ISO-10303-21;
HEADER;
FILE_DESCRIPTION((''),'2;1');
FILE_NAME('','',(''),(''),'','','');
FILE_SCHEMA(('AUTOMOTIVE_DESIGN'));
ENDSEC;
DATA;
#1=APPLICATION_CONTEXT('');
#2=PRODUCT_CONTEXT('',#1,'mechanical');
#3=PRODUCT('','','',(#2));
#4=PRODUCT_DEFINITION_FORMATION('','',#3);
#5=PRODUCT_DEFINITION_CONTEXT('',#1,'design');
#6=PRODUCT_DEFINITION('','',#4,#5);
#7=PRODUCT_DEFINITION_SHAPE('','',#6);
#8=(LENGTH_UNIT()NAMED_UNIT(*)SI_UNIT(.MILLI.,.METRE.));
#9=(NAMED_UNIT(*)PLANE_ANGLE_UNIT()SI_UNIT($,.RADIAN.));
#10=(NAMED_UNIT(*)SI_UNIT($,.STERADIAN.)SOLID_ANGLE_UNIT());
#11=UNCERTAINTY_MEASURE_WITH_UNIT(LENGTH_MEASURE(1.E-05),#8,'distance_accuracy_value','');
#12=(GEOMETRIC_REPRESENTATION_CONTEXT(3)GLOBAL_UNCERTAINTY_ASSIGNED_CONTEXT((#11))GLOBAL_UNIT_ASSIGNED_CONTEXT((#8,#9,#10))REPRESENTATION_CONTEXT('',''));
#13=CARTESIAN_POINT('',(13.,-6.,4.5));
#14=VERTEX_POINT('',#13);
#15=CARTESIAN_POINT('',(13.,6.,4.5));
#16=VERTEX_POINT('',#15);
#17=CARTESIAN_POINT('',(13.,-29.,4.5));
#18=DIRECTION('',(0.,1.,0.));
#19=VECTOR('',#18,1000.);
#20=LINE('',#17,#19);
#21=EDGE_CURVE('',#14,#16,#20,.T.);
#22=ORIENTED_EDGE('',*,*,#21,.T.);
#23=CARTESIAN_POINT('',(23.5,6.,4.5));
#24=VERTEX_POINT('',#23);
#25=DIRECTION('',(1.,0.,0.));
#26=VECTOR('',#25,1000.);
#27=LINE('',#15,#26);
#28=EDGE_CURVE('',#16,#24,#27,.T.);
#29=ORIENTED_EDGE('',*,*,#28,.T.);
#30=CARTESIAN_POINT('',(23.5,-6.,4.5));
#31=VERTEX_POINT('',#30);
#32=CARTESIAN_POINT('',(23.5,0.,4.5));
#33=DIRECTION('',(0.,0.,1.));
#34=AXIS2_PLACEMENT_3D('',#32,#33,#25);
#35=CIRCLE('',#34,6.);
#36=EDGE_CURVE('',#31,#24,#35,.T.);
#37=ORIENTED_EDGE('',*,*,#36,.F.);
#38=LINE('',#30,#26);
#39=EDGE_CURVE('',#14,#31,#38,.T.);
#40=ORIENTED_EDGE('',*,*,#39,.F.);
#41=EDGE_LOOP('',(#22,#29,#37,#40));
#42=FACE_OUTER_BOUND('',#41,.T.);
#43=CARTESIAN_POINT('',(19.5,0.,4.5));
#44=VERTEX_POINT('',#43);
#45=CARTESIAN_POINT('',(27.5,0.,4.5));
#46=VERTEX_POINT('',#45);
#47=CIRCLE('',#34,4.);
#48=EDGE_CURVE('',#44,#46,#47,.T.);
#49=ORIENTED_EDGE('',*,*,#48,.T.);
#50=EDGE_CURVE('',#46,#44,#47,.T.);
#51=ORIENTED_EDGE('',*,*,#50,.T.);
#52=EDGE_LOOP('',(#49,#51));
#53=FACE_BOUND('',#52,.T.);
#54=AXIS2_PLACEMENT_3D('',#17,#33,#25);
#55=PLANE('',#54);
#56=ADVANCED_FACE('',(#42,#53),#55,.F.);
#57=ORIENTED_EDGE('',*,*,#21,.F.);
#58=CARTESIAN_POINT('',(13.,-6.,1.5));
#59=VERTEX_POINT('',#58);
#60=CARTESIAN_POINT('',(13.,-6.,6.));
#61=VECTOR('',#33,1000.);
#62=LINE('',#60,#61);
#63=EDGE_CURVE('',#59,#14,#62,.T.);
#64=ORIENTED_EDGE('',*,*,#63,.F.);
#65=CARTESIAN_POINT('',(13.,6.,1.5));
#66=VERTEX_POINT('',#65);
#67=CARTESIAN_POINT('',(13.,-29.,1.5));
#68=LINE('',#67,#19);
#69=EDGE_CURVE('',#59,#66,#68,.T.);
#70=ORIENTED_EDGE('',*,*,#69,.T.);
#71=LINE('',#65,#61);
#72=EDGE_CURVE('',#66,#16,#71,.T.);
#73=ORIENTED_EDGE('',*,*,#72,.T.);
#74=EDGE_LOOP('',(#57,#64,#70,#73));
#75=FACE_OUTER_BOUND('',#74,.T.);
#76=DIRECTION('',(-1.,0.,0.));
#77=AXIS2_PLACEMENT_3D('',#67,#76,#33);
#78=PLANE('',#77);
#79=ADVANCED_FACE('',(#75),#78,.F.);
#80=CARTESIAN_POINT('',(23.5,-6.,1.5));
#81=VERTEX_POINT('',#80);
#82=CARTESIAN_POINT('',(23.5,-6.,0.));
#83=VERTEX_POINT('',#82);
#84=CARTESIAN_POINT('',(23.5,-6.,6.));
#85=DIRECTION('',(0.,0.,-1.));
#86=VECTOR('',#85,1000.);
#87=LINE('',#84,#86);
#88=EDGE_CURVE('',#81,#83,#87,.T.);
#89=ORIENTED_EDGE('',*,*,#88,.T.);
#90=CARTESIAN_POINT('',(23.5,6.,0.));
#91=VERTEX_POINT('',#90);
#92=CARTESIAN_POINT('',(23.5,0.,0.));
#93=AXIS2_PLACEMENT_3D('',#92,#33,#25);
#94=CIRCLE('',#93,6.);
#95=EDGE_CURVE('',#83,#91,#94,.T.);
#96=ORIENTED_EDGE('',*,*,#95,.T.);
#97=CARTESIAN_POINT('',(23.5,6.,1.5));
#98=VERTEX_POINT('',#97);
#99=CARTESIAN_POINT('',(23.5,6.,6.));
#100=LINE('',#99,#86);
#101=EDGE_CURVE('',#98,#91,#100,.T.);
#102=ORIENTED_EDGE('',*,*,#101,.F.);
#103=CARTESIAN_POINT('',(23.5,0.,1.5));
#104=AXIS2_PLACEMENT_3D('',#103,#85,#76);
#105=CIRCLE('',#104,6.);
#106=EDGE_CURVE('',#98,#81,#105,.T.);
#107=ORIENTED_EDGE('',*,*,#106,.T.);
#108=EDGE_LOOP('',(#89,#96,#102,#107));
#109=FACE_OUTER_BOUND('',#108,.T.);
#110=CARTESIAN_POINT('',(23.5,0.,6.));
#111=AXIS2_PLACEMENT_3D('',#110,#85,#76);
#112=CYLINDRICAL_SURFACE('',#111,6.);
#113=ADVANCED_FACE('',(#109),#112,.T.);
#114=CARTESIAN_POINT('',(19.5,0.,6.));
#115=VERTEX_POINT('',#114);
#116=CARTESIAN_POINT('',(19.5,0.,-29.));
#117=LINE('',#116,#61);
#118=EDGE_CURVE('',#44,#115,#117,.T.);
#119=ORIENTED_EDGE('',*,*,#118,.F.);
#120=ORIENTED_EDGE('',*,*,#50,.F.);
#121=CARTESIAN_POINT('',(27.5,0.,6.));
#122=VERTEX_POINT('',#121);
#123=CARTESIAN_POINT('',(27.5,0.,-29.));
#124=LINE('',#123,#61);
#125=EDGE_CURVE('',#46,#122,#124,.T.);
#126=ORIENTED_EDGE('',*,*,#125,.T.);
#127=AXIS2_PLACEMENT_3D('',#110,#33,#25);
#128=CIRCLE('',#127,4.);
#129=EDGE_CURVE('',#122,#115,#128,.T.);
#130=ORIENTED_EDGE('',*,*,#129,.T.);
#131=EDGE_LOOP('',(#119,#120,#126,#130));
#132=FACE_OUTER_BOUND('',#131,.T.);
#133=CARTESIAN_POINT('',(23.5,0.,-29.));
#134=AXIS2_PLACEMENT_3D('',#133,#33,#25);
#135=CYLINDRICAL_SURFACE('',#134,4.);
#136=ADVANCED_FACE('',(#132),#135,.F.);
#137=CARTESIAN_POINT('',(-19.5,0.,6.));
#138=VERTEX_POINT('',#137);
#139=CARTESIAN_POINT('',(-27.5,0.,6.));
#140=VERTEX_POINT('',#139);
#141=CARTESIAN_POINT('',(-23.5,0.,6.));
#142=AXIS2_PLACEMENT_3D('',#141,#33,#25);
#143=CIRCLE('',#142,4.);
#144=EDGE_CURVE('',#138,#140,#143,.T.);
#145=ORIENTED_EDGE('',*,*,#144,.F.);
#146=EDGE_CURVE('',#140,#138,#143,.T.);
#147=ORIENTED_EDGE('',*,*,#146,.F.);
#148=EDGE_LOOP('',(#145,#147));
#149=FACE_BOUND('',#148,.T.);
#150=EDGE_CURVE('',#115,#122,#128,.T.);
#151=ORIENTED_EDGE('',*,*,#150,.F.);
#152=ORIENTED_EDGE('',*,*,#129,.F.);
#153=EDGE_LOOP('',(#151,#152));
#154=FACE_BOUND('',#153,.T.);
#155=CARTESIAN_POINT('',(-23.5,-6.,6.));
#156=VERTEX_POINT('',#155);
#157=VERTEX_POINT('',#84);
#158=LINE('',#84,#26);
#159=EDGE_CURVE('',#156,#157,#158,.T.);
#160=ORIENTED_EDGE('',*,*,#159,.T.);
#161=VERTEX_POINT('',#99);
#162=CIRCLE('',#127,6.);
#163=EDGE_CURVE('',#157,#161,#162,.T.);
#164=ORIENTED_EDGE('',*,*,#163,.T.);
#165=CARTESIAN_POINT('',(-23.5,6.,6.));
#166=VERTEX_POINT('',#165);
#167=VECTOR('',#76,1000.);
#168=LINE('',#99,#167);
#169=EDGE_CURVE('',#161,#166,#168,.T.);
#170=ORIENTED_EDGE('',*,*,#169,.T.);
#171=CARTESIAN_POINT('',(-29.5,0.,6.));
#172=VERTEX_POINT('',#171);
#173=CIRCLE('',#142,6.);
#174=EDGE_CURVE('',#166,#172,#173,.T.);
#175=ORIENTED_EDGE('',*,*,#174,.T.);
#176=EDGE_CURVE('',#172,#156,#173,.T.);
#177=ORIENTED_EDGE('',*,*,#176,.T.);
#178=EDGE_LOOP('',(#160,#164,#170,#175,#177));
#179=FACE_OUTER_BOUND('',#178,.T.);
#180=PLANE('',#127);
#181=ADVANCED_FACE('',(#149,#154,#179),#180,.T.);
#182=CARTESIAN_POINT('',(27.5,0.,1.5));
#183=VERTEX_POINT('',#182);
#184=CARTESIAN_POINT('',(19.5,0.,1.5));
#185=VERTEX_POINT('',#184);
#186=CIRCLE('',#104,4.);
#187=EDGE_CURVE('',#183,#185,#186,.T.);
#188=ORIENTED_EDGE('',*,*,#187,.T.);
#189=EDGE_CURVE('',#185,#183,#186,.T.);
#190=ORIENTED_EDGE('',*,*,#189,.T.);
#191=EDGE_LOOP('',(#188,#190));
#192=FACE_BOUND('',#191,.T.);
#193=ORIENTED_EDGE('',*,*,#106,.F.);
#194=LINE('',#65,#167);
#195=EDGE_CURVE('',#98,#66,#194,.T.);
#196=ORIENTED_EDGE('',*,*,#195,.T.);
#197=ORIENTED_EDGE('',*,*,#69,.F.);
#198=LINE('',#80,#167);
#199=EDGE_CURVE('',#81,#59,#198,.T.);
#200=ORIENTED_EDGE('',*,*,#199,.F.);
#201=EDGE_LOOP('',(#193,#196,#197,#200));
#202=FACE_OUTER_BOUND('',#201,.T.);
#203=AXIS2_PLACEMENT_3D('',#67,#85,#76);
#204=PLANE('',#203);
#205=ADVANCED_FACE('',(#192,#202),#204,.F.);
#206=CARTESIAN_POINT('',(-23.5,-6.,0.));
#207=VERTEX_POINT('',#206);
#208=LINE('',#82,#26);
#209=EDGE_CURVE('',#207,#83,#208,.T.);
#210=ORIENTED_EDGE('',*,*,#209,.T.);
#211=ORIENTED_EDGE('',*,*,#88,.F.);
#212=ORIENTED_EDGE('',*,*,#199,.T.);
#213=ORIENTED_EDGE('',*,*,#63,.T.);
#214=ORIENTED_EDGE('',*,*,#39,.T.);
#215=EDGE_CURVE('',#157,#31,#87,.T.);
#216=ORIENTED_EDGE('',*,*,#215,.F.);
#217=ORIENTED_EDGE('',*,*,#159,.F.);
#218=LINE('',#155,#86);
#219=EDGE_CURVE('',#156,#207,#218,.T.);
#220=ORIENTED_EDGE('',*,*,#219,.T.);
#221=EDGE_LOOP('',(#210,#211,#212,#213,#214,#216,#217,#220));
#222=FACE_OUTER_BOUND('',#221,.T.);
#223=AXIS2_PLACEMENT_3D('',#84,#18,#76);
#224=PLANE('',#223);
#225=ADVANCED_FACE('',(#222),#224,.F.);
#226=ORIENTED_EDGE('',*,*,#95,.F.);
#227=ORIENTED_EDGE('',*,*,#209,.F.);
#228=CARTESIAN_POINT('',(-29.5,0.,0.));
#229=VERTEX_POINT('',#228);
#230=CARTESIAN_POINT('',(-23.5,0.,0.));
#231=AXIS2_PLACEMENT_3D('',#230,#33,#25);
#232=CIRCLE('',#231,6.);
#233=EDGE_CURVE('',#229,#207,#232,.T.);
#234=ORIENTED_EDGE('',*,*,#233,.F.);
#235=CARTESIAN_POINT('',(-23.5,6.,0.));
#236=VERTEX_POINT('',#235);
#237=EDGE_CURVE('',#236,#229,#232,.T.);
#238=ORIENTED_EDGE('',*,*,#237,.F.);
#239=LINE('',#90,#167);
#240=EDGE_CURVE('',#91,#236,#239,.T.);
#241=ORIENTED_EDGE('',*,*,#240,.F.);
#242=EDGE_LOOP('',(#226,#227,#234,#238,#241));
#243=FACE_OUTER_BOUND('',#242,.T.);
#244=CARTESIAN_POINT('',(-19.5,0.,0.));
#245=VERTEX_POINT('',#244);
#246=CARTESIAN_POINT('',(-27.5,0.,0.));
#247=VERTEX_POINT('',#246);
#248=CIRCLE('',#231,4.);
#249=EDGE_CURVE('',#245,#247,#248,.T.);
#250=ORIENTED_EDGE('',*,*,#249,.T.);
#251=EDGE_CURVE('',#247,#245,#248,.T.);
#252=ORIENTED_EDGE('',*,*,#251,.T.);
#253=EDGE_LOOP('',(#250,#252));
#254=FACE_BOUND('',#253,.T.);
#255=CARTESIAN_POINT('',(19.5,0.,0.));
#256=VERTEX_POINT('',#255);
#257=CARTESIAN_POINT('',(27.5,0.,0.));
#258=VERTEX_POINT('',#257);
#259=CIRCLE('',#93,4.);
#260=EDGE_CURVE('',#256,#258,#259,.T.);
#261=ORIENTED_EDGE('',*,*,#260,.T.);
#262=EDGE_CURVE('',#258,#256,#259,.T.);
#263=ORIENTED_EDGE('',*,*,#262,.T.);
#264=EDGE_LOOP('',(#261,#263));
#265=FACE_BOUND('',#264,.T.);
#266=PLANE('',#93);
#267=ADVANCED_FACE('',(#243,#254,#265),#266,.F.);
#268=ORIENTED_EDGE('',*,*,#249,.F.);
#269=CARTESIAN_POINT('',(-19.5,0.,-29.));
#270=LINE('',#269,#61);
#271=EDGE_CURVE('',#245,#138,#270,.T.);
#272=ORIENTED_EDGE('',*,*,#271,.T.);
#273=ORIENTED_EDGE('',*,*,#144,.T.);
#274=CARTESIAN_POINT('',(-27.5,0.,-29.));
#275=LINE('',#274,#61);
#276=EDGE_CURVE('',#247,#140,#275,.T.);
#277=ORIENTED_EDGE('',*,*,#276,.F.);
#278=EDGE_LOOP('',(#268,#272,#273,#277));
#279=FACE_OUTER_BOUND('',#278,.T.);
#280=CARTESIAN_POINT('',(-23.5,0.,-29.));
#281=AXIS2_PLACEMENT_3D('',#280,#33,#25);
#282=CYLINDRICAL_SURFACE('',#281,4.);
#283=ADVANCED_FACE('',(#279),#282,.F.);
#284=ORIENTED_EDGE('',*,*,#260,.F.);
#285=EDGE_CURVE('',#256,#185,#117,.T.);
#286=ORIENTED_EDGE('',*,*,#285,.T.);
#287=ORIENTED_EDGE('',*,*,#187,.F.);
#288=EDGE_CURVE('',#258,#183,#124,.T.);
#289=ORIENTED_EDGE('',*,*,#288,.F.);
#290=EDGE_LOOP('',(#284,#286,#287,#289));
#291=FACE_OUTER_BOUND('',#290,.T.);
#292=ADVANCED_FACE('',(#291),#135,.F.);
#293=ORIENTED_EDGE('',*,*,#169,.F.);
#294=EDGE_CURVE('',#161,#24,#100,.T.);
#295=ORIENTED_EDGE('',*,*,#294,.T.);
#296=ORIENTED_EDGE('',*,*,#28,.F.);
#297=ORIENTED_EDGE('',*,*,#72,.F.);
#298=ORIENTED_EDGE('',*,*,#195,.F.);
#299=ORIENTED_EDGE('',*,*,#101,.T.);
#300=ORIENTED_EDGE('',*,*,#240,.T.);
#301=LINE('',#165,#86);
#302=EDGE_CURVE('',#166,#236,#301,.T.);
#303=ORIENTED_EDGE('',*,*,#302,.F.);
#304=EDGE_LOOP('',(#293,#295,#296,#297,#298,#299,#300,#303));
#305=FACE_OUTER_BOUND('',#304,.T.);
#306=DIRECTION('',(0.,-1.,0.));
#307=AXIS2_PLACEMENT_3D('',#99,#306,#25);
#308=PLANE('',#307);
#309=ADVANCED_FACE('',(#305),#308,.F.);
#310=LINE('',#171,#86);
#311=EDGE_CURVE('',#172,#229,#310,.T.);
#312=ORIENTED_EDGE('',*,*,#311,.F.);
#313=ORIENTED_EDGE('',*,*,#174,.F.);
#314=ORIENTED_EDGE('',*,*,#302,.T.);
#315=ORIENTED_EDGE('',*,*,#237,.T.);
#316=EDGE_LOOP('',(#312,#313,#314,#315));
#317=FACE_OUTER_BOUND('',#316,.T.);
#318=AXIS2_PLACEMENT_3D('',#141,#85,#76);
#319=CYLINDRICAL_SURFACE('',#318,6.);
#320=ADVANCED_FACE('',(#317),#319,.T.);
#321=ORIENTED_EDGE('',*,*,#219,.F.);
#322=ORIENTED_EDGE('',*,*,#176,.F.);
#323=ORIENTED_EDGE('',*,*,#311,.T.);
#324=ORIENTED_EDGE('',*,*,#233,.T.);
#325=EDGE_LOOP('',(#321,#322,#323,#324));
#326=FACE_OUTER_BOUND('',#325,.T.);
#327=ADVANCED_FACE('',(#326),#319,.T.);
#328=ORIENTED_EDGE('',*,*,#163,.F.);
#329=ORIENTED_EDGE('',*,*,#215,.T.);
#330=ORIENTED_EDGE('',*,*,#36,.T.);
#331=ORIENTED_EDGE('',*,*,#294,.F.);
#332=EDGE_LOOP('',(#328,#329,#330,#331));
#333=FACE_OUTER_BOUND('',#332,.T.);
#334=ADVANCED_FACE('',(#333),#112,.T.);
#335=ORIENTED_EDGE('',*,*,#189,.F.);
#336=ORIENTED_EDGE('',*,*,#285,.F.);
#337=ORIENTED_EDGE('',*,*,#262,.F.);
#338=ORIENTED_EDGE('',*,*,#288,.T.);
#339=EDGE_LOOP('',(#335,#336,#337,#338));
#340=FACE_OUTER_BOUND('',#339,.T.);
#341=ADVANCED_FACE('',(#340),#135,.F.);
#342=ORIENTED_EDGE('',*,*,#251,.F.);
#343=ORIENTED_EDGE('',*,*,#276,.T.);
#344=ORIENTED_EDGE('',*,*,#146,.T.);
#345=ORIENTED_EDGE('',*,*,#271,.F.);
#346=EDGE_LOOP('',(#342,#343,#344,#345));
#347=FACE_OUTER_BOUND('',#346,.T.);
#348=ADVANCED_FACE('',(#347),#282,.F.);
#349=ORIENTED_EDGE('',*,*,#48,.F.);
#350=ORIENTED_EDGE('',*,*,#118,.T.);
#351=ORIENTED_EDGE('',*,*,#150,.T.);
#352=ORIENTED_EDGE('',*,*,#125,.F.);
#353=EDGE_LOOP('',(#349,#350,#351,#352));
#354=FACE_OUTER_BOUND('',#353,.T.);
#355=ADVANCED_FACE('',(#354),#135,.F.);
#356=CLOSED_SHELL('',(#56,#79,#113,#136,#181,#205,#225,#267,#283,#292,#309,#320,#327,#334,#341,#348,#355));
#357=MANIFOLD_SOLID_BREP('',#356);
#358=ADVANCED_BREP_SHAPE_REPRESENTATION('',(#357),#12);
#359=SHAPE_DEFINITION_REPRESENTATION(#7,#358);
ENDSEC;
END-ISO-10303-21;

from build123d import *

# Parameters (mm, degrees)
BOSS_EXTRUDE1_DEPTH = 6
SKETCH2_W           = 33
SKETCH2_H           = 3
CUT_EXTRUDE1_DEPTH  = 35
SKETCH3_R           = 4
CUT_EXTRUDE2_DEPTH  = 35


with BuildPart() as part:
    # Sketch1 → Boss-Extrude1 (new body)
    with BuildSketch(Plane.XY):
        with BuildLine():
            Line((23.5, -6), (-23.5, -6))
            ThreePointArc((-23.5, -6), (-29.5, 0), (-23.5, 6))
            Line((-23.5, 6), (23.5, 6))
            ThreePointArc((23.5, 6), (29.5, 0), (23.5, -6))
        make_face()
    extrude(amount=BOSS_EXTRUDE1_DEPTH)

    # Sketch2 → Cut-Extrude1 (cut)
    with BuildSketch(Plane(origin=(0, 6, 0), x_dir=(1, 0, 0), z_dir=(0, 1, 0))):
        with Locations((29.5, -3)):
            Rectangle(SKETCH2_W, SKETCH2_H)
    extrude(amount=-CUT_EXTRUDE1_DEPTH, mode=Mode.SUBTRACT)

    # Sketch3 → Cut-Extrude2 (cut)
    with BuildSketch(Plane.XY.offset(6)):
        with Locations((23.5, 0)):
            Circle(SKETCH3_R)
        with Locations((-23.5, 0)):
            Circle(SKETCH3_R)
    extrude(amount=-CUT_EXTRUDE2_DEPTH, mode=Mode.SUBTRACT)


solid = part.part
